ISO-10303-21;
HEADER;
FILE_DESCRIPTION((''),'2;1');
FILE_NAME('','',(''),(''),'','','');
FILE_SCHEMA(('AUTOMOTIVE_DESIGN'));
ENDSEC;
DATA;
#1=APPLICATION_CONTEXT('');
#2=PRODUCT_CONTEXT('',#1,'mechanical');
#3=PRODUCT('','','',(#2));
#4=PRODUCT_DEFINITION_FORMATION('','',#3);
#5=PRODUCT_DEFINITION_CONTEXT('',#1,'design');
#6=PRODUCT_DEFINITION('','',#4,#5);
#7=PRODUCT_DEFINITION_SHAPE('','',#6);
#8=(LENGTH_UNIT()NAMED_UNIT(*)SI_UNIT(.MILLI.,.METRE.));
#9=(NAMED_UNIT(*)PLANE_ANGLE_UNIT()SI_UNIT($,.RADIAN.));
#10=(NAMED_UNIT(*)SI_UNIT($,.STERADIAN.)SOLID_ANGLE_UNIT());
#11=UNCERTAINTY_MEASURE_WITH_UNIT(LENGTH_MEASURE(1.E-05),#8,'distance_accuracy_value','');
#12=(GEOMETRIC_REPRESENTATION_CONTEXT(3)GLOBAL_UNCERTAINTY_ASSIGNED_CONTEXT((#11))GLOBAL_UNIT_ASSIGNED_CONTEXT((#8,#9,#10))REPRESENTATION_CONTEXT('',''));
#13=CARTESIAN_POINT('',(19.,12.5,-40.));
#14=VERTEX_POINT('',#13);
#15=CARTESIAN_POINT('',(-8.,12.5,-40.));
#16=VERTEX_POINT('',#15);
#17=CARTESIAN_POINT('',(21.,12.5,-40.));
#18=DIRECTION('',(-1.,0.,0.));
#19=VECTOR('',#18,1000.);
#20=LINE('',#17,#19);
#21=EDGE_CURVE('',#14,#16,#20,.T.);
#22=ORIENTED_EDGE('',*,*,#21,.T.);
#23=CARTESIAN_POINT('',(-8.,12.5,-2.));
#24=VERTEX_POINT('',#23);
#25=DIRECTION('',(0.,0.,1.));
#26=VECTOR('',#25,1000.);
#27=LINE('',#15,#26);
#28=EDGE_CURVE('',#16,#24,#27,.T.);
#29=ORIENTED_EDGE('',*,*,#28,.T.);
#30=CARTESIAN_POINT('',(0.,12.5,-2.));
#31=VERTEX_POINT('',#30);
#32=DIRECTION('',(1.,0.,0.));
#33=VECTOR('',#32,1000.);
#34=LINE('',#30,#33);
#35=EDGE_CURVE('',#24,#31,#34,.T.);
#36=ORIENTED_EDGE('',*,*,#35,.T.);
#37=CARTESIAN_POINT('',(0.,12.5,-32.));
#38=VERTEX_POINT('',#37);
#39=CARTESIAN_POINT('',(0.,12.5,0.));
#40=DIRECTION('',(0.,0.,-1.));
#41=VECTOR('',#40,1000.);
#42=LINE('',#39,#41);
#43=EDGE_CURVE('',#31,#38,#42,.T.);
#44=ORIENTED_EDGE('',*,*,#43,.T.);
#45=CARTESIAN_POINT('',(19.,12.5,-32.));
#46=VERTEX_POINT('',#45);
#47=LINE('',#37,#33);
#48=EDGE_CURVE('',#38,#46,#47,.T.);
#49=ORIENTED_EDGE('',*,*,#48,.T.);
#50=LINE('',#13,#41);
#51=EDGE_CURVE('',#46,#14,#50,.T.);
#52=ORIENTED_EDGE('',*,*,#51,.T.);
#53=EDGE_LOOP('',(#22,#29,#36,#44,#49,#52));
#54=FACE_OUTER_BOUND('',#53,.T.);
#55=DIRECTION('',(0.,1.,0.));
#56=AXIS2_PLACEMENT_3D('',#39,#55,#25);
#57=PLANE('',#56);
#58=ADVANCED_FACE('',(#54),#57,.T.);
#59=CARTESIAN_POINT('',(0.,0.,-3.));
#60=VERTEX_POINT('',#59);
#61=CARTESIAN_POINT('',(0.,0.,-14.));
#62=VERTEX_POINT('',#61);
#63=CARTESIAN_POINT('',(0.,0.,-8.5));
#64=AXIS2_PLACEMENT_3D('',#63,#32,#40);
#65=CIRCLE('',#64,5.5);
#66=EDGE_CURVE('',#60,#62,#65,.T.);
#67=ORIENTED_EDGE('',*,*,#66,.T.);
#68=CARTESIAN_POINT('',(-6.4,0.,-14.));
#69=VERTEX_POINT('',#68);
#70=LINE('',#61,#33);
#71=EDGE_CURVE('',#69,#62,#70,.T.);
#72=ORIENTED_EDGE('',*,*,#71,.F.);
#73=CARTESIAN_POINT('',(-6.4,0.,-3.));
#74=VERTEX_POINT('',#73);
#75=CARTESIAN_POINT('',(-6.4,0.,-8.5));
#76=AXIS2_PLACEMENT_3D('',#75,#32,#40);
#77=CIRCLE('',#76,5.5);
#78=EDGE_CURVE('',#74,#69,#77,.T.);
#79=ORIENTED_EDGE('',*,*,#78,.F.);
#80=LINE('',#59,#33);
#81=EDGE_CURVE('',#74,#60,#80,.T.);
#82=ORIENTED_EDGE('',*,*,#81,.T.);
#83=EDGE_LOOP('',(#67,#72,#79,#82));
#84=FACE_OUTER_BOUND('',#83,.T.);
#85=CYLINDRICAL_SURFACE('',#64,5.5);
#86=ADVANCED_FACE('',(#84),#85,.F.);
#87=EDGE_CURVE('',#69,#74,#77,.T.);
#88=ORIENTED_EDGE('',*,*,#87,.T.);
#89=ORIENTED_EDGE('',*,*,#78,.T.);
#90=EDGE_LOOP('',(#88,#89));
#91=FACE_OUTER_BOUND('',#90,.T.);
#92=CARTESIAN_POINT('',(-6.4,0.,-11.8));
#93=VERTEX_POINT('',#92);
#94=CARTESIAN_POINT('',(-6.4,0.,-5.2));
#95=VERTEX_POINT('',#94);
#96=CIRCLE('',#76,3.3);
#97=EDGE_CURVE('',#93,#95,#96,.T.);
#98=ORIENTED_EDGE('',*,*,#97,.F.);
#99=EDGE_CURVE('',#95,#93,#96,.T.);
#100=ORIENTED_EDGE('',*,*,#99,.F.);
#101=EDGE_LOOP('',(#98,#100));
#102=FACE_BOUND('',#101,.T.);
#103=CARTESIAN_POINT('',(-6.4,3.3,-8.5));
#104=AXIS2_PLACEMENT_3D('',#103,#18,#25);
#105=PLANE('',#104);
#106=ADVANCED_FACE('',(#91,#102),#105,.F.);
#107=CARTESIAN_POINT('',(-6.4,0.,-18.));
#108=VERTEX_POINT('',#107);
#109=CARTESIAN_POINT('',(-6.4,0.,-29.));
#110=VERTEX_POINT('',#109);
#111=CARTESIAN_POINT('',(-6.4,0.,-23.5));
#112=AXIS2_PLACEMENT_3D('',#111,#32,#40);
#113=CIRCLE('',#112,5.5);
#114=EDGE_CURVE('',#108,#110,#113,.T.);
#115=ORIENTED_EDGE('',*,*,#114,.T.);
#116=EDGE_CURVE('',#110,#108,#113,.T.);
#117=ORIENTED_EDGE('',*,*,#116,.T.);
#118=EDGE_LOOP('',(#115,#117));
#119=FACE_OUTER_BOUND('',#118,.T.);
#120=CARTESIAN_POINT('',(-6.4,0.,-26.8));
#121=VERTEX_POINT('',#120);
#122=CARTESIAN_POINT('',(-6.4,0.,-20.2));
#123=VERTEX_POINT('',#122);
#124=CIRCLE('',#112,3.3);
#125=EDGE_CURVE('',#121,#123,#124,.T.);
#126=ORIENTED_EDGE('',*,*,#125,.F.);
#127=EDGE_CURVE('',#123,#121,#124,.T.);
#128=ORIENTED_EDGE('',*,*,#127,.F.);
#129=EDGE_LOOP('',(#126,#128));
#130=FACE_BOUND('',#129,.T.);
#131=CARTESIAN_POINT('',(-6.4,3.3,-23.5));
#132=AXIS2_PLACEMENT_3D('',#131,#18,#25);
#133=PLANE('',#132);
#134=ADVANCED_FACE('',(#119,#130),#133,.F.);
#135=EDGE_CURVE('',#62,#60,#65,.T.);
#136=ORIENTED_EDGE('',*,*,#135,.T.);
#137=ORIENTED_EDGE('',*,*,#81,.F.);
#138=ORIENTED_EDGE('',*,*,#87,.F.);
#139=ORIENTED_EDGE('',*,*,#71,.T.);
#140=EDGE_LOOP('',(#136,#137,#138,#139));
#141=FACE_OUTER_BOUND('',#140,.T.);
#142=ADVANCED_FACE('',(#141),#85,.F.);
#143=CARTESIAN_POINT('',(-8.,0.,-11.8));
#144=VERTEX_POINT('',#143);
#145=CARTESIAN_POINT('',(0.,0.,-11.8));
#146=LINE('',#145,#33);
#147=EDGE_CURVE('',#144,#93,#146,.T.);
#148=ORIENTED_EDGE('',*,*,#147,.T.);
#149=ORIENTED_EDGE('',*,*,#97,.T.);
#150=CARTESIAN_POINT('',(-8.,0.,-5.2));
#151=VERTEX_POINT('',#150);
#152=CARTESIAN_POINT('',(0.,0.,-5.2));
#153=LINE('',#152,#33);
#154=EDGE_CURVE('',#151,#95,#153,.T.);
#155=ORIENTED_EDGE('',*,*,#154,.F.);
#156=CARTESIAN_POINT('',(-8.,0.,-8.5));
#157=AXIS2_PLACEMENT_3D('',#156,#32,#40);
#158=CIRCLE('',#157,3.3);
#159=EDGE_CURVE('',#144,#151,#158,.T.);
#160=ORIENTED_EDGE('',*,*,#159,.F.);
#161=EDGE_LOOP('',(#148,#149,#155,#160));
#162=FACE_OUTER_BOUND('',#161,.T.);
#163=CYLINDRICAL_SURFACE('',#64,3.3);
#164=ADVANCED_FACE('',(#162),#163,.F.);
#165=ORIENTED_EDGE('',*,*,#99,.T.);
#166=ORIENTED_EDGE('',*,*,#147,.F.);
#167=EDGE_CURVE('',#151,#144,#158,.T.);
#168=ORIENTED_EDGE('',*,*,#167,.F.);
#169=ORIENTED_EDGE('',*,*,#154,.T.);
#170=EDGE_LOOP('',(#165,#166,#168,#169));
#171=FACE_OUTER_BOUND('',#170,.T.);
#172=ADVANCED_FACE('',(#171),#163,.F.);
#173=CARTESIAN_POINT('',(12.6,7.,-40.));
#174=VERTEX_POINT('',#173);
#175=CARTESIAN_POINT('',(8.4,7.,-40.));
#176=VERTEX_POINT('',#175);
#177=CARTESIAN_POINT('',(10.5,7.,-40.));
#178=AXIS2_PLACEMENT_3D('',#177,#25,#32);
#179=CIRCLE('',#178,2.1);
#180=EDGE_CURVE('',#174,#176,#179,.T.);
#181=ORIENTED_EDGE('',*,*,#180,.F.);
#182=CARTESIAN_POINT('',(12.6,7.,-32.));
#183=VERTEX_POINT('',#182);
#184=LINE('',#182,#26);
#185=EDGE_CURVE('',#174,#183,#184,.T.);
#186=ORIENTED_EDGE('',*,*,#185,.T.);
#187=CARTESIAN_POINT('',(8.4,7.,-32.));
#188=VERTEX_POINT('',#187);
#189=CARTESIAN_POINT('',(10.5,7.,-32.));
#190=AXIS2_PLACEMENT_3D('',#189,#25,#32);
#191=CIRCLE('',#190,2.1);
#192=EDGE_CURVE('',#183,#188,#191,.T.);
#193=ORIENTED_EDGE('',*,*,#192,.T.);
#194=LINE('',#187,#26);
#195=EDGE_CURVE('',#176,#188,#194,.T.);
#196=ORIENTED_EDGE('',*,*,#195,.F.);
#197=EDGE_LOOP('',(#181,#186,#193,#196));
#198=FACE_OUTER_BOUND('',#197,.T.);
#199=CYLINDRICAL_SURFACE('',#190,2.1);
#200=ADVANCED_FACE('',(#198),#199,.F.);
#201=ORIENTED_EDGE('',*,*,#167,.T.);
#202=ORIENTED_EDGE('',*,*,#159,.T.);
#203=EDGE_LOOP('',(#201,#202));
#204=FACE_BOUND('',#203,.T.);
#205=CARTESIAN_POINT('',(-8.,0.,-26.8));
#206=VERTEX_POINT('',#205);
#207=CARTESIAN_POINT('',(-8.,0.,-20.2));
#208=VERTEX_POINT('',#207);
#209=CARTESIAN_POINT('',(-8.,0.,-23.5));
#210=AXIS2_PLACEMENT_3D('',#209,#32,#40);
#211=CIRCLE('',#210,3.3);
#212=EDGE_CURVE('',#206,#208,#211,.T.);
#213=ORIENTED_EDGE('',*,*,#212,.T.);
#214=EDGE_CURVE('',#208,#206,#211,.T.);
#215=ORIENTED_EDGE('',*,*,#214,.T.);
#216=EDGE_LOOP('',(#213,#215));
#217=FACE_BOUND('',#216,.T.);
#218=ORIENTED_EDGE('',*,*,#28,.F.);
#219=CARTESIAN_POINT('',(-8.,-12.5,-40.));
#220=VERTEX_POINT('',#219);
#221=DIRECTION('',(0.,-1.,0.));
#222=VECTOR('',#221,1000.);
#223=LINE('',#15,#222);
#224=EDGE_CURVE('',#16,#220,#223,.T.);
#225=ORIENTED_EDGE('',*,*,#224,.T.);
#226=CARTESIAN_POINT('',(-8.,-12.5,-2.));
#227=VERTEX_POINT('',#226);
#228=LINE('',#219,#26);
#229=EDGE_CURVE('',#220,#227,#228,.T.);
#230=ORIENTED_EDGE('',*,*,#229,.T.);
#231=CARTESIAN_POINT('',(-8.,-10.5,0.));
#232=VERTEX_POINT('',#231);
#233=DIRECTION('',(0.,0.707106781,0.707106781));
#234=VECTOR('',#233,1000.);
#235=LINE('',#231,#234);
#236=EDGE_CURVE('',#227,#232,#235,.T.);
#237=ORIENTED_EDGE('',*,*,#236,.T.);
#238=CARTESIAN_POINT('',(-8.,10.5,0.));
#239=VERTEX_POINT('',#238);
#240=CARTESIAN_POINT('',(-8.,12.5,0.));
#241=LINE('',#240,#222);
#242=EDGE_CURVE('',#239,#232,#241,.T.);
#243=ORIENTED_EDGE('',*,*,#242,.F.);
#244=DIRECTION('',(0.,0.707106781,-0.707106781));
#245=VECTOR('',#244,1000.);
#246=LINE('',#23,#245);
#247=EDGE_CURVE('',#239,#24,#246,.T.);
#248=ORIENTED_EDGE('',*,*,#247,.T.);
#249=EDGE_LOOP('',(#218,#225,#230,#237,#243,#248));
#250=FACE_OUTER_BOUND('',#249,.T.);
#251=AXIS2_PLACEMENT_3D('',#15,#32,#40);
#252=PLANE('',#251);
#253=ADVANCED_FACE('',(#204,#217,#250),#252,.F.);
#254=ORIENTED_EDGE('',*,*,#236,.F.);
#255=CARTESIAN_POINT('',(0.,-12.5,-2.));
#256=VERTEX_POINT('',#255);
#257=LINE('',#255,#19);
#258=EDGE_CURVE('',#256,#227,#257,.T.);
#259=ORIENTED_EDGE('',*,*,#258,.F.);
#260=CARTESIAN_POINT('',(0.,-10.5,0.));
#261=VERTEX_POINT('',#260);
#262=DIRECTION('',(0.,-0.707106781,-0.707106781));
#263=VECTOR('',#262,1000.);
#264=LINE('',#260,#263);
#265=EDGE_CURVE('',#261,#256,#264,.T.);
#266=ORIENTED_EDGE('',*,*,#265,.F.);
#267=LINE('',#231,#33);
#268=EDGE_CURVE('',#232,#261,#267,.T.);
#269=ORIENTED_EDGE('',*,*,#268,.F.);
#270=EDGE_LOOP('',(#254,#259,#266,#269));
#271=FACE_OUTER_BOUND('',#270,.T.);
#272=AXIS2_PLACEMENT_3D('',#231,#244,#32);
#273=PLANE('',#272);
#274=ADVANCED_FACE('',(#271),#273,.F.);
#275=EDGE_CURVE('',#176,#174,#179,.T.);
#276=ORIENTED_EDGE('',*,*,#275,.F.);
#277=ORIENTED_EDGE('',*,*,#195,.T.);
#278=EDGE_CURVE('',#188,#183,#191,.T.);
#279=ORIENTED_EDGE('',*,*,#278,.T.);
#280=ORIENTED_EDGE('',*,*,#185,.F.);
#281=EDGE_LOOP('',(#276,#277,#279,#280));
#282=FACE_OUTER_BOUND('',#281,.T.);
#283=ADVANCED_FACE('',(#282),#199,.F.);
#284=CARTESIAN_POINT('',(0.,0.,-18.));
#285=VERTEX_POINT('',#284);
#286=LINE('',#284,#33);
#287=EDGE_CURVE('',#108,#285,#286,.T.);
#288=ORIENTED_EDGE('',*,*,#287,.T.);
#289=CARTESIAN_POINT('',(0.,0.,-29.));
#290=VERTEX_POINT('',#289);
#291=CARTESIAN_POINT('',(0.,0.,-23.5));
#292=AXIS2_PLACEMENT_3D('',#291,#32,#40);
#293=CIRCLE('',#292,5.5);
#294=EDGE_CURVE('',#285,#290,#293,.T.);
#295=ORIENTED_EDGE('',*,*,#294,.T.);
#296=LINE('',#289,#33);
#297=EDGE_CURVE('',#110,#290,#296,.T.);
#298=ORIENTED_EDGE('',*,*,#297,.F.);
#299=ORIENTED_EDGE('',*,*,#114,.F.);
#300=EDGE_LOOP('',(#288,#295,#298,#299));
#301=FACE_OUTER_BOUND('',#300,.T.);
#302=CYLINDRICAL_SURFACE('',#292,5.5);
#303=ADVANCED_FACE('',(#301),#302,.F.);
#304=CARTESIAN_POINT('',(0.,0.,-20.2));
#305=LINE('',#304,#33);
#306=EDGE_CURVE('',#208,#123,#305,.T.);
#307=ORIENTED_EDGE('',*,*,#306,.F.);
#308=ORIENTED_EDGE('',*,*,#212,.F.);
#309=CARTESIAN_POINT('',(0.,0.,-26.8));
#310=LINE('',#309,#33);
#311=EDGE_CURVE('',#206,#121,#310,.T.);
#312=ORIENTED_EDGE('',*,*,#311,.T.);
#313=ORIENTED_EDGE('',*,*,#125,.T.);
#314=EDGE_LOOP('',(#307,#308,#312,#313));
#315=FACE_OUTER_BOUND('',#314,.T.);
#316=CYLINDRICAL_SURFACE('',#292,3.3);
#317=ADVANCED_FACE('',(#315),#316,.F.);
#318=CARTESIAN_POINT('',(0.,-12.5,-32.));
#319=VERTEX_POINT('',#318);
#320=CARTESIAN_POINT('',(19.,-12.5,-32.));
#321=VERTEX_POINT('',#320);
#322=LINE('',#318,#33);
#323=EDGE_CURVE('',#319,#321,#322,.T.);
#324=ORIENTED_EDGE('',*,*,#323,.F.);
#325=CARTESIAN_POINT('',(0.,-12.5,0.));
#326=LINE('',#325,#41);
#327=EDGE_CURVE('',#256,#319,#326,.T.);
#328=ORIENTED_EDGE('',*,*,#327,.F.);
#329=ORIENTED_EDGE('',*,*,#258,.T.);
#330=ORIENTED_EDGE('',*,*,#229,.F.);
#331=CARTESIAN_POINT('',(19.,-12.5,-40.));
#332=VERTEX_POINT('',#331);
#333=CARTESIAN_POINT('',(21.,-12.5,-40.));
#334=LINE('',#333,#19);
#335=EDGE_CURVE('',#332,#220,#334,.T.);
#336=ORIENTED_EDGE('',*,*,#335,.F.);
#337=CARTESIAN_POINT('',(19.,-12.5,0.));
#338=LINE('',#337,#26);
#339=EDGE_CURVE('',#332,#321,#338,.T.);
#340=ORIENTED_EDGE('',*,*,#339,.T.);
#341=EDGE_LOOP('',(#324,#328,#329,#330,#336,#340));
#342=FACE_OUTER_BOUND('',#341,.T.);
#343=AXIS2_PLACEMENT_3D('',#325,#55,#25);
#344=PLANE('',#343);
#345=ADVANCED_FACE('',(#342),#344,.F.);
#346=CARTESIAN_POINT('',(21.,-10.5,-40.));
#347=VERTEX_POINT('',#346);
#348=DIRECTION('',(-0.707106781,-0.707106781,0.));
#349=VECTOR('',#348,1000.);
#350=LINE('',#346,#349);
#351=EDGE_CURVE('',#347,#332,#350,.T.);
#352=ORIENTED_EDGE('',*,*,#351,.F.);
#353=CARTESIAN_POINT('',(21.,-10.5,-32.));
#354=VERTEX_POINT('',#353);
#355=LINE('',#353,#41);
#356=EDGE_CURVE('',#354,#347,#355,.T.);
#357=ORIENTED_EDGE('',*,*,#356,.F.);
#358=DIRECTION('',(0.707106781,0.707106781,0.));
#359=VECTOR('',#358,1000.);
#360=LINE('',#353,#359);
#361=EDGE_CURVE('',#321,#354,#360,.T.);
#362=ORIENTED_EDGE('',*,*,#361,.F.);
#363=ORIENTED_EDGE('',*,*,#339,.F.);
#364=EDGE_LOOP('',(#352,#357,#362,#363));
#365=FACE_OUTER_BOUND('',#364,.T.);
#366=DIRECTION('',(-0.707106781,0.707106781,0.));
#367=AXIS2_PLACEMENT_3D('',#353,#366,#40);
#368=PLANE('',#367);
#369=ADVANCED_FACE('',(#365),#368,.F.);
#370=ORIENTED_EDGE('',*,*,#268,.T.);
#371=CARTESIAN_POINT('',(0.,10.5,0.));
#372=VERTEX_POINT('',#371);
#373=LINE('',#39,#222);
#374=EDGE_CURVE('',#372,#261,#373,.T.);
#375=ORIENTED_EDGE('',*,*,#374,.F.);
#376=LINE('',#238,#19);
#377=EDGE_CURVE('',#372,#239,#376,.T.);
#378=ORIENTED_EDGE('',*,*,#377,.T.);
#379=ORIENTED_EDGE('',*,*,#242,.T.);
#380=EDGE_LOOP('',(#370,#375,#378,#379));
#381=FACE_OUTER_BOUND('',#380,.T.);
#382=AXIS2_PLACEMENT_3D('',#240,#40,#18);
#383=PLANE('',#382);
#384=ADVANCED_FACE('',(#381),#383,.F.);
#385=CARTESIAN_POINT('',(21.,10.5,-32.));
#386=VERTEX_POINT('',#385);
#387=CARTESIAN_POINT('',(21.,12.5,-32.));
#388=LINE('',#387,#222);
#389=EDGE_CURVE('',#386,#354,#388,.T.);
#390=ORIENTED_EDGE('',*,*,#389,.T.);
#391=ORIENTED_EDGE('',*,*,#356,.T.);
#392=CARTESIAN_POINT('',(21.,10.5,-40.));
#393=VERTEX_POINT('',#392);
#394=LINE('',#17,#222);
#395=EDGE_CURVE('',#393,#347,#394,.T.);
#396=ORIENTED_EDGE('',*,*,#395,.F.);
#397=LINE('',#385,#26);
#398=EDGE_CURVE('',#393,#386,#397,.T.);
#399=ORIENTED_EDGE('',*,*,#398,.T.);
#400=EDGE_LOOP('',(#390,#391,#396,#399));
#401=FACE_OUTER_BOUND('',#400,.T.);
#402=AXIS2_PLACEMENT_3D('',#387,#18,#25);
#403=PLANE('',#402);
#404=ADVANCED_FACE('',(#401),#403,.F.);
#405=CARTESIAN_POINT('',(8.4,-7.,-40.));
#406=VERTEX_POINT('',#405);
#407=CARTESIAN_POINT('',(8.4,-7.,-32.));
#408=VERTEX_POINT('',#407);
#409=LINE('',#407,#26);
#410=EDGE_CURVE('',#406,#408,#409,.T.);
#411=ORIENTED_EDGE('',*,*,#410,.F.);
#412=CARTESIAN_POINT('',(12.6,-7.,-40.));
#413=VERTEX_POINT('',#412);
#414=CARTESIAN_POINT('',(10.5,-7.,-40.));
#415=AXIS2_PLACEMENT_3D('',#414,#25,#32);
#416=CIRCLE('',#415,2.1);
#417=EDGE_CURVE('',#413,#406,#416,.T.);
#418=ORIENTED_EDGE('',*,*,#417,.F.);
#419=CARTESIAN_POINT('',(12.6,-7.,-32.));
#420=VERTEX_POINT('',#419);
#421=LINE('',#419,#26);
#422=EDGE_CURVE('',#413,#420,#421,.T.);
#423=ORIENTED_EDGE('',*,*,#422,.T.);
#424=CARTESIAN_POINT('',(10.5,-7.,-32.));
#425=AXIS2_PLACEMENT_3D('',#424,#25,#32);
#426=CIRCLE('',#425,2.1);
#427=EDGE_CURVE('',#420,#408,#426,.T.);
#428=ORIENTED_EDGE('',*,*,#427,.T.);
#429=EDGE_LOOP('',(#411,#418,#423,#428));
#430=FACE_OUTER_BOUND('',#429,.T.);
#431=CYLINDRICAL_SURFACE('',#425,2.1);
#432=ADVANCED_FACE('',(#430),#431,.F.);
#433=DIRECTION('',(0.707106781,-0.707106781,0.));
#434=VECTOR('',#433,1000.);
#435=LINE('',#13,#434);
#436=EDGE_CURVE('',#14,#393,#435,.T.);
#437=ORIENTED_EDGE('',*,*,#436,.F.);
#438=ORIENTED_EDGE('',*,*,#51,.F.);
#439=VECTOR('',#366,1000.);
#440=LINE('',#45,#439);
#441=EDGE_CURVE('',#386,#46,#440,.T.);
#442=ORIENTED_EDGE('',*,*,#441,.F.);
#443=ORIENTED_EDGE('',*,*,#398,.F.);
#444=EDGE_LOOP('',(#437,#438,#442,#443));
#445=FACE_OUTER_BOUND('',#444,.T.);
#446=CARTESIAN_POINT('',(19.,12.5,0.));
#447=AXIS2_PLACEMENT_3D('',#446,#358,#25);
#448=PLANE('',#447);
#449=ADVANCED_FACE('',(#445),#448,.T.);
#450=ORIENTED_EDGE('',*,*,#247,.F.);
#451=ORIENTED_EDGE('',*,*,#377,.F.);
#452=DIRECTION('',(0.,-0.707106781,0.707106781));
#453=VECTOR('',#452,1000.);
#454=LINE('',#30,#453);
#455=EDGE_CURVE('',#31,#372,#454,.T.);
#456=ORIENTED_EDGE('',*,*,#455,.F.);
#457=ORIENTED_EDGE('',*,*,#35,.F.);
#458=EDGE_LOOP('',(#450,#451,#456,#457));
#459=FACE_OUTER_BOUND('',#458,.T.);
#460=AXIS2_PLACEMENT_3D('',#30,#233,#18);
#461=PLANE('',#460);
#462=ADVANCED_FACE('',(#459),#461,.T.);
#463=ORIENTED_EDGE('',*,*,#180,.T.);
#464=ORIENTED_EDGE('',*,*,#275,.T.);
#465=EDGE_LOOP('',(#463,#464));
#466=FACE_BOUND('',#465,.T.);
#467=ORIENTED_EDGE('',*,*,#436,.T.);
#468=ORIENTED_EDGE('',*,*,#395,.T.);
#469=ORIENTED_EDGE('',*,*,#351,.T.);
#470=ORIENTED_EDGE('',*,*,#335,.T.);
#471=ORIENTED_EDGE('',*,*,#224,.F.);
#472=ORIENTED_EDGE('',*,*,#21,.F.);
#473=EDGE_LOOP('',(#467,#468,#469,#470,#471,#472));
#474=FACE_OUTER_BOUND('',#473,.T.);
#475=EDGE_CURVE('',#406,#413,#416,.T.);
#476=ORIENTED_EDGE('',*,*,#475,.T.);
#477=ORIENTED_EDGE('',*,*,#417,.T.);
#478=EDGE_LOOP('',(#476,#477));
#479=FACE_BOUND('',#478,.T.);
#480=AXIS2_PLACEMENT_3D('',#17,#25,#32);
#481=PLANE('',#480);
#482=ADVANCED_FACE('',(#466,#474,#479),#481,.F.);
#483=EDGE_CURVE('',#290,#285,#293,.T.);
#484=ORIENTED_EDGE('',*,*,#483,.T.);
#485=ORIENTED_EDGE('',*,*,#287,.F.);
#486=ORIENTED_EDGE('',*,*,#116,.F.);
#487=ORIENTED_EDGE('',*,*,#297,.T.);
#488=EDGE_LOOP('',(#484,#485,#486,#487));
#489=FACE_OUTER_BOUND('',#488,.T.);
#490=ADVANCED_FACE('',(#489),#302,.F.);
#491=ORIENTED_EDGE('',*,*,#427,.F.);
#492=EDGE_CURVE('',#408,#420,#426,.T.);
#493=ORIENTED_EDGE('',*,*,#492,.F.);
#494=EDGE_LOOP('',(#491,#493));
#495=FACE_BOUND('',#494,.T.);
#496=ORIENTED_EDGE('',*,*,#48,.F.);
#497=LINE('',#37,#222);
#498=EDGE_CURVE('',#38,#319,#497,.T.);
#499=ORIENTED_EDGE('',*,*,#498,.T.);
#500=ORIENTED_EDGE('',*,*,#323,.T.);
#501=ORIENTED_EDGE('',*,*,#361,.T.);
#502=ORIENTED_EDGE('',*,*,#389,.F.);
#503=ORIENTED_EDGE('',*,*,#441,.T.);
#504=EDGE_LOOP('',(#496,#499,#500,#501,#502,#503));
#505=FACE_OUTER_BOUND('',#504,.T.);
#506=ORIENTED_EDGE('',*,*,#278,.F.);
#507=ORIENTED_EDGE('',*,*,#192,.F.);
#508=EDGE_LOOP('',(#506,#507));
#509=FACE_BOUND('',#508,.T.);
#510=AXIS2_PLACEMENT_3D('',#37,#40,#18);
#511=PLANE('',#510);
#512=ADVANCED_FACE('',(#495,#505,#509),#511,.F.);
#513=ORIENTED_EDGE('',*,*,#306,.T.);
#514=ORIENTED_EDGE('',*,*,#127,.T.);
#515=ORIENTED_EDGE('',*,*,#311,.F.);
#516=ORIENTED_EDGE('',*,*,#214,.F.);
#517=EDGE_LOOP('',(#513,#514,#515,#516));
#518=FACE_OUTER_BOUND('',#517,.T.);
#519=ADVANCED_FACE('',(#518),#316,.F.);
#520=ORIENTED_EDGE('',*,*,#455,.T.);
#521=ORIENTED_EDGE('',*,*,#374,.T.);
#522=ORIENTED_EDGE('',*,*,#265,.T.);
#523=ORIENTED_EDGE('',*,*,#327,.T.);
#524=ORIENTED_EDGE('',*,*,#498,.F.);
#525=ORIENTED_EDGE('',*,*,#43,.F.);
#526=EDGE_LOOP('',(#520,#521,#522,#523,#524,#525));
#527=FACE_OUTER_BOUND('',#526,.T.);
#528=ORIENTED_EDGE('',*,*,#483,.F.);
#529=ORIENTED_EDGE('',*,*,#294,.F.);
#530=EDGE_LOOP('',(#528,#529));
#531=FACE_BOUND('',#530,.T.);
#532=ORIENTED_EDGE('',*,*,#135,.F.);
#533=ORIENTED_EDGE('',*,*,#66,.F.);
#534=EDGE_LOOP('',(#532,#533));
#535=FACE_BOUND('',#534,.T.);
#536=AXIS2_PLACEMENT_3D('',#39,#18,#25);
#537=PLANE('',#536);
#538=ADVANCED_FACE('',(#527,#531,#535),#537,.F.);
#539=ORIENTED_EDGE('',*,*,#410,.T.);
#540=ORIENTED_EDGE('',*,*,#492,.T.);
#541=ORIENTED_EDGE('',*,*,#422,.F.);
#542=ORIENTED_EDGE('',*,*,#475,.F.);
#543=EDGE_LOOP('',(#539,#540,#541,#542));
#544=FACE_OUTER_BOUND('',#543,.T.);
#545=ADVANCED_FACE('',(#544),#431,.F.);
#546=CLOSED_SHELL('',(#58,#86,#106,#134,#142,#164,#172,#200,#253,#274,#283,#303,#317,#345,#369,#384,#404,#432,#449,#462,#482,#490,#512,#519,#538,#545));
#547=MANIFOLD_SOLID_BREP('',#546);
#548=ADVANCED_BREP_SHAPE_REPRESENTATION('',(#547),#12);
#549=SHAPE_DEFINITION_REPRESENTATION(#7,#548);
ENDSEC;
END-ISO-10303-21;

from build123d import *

# Parameters (mm, degrees)
EXTRUDE_1_DEPTH              = 12.5
HOLE_WIZARD_M5_1_D           = 4.2
HOLE_WIZARD_M6_1_D           = 6.6
HOLE_WIZARD_M6_1_CBORE_D     = 11
HOLE_WIZARD_M6_1_CBORE_DEPTH = 6.4
CHAMFER_1_SIZE               = 2


with BuildPart() as part:
    # 草图1 → 凸台-拉伸1 (new, symmetric)
    with BuildSketch(Plane(origin=(0, 0, 0), x_dir=(1, 0, 0), z_dir=(0, 1, 0))):
        Polygon((0, 0), (0, 32), (21, 32), (21, 40), (-8, 40), (-8, 0), align=None)
    extrude(amount=EXTRUDE_1_DEPTH, both=True)

    # M5 螺纹孔1 (through all)
    with Locations(Plane.XY.offset(-32)):
        with Locations((10.5, 7), (10.5, -7)):
            Hole(HOLE_WIZARD_M5_1_D / 2)

    # M6 六角凹头螺钉的柱形沉头孔1 (through all)
    with Locations(Plane(origin=(0, 0, 0), x_dir=(0, 0, -1), z_dir=(1, 0, 0))):
        with Locations((8.5, 0), (23.5, 0)):
            CounterBoreHole(HOLE_WIZARD_M6_1_D / 2, HOLE_WIZARD_M6_1_CBORE_D / 2, HOLE_WIZARD_M6_1_CBORE_DEPTH)

    # 倒角1
    chamfer_1_edges = [part.edges().sort_by_distance(p)[0] for p in [
        (21, 12.5, -36),
        (-4, 12.5, 0),
        (21, -12.5, -36),
        (-4, -12.5, 0),
    ]]
    chamfer(chamfer_1_edges, length=CHAMFER_1_SIZE)


solid = part.part
